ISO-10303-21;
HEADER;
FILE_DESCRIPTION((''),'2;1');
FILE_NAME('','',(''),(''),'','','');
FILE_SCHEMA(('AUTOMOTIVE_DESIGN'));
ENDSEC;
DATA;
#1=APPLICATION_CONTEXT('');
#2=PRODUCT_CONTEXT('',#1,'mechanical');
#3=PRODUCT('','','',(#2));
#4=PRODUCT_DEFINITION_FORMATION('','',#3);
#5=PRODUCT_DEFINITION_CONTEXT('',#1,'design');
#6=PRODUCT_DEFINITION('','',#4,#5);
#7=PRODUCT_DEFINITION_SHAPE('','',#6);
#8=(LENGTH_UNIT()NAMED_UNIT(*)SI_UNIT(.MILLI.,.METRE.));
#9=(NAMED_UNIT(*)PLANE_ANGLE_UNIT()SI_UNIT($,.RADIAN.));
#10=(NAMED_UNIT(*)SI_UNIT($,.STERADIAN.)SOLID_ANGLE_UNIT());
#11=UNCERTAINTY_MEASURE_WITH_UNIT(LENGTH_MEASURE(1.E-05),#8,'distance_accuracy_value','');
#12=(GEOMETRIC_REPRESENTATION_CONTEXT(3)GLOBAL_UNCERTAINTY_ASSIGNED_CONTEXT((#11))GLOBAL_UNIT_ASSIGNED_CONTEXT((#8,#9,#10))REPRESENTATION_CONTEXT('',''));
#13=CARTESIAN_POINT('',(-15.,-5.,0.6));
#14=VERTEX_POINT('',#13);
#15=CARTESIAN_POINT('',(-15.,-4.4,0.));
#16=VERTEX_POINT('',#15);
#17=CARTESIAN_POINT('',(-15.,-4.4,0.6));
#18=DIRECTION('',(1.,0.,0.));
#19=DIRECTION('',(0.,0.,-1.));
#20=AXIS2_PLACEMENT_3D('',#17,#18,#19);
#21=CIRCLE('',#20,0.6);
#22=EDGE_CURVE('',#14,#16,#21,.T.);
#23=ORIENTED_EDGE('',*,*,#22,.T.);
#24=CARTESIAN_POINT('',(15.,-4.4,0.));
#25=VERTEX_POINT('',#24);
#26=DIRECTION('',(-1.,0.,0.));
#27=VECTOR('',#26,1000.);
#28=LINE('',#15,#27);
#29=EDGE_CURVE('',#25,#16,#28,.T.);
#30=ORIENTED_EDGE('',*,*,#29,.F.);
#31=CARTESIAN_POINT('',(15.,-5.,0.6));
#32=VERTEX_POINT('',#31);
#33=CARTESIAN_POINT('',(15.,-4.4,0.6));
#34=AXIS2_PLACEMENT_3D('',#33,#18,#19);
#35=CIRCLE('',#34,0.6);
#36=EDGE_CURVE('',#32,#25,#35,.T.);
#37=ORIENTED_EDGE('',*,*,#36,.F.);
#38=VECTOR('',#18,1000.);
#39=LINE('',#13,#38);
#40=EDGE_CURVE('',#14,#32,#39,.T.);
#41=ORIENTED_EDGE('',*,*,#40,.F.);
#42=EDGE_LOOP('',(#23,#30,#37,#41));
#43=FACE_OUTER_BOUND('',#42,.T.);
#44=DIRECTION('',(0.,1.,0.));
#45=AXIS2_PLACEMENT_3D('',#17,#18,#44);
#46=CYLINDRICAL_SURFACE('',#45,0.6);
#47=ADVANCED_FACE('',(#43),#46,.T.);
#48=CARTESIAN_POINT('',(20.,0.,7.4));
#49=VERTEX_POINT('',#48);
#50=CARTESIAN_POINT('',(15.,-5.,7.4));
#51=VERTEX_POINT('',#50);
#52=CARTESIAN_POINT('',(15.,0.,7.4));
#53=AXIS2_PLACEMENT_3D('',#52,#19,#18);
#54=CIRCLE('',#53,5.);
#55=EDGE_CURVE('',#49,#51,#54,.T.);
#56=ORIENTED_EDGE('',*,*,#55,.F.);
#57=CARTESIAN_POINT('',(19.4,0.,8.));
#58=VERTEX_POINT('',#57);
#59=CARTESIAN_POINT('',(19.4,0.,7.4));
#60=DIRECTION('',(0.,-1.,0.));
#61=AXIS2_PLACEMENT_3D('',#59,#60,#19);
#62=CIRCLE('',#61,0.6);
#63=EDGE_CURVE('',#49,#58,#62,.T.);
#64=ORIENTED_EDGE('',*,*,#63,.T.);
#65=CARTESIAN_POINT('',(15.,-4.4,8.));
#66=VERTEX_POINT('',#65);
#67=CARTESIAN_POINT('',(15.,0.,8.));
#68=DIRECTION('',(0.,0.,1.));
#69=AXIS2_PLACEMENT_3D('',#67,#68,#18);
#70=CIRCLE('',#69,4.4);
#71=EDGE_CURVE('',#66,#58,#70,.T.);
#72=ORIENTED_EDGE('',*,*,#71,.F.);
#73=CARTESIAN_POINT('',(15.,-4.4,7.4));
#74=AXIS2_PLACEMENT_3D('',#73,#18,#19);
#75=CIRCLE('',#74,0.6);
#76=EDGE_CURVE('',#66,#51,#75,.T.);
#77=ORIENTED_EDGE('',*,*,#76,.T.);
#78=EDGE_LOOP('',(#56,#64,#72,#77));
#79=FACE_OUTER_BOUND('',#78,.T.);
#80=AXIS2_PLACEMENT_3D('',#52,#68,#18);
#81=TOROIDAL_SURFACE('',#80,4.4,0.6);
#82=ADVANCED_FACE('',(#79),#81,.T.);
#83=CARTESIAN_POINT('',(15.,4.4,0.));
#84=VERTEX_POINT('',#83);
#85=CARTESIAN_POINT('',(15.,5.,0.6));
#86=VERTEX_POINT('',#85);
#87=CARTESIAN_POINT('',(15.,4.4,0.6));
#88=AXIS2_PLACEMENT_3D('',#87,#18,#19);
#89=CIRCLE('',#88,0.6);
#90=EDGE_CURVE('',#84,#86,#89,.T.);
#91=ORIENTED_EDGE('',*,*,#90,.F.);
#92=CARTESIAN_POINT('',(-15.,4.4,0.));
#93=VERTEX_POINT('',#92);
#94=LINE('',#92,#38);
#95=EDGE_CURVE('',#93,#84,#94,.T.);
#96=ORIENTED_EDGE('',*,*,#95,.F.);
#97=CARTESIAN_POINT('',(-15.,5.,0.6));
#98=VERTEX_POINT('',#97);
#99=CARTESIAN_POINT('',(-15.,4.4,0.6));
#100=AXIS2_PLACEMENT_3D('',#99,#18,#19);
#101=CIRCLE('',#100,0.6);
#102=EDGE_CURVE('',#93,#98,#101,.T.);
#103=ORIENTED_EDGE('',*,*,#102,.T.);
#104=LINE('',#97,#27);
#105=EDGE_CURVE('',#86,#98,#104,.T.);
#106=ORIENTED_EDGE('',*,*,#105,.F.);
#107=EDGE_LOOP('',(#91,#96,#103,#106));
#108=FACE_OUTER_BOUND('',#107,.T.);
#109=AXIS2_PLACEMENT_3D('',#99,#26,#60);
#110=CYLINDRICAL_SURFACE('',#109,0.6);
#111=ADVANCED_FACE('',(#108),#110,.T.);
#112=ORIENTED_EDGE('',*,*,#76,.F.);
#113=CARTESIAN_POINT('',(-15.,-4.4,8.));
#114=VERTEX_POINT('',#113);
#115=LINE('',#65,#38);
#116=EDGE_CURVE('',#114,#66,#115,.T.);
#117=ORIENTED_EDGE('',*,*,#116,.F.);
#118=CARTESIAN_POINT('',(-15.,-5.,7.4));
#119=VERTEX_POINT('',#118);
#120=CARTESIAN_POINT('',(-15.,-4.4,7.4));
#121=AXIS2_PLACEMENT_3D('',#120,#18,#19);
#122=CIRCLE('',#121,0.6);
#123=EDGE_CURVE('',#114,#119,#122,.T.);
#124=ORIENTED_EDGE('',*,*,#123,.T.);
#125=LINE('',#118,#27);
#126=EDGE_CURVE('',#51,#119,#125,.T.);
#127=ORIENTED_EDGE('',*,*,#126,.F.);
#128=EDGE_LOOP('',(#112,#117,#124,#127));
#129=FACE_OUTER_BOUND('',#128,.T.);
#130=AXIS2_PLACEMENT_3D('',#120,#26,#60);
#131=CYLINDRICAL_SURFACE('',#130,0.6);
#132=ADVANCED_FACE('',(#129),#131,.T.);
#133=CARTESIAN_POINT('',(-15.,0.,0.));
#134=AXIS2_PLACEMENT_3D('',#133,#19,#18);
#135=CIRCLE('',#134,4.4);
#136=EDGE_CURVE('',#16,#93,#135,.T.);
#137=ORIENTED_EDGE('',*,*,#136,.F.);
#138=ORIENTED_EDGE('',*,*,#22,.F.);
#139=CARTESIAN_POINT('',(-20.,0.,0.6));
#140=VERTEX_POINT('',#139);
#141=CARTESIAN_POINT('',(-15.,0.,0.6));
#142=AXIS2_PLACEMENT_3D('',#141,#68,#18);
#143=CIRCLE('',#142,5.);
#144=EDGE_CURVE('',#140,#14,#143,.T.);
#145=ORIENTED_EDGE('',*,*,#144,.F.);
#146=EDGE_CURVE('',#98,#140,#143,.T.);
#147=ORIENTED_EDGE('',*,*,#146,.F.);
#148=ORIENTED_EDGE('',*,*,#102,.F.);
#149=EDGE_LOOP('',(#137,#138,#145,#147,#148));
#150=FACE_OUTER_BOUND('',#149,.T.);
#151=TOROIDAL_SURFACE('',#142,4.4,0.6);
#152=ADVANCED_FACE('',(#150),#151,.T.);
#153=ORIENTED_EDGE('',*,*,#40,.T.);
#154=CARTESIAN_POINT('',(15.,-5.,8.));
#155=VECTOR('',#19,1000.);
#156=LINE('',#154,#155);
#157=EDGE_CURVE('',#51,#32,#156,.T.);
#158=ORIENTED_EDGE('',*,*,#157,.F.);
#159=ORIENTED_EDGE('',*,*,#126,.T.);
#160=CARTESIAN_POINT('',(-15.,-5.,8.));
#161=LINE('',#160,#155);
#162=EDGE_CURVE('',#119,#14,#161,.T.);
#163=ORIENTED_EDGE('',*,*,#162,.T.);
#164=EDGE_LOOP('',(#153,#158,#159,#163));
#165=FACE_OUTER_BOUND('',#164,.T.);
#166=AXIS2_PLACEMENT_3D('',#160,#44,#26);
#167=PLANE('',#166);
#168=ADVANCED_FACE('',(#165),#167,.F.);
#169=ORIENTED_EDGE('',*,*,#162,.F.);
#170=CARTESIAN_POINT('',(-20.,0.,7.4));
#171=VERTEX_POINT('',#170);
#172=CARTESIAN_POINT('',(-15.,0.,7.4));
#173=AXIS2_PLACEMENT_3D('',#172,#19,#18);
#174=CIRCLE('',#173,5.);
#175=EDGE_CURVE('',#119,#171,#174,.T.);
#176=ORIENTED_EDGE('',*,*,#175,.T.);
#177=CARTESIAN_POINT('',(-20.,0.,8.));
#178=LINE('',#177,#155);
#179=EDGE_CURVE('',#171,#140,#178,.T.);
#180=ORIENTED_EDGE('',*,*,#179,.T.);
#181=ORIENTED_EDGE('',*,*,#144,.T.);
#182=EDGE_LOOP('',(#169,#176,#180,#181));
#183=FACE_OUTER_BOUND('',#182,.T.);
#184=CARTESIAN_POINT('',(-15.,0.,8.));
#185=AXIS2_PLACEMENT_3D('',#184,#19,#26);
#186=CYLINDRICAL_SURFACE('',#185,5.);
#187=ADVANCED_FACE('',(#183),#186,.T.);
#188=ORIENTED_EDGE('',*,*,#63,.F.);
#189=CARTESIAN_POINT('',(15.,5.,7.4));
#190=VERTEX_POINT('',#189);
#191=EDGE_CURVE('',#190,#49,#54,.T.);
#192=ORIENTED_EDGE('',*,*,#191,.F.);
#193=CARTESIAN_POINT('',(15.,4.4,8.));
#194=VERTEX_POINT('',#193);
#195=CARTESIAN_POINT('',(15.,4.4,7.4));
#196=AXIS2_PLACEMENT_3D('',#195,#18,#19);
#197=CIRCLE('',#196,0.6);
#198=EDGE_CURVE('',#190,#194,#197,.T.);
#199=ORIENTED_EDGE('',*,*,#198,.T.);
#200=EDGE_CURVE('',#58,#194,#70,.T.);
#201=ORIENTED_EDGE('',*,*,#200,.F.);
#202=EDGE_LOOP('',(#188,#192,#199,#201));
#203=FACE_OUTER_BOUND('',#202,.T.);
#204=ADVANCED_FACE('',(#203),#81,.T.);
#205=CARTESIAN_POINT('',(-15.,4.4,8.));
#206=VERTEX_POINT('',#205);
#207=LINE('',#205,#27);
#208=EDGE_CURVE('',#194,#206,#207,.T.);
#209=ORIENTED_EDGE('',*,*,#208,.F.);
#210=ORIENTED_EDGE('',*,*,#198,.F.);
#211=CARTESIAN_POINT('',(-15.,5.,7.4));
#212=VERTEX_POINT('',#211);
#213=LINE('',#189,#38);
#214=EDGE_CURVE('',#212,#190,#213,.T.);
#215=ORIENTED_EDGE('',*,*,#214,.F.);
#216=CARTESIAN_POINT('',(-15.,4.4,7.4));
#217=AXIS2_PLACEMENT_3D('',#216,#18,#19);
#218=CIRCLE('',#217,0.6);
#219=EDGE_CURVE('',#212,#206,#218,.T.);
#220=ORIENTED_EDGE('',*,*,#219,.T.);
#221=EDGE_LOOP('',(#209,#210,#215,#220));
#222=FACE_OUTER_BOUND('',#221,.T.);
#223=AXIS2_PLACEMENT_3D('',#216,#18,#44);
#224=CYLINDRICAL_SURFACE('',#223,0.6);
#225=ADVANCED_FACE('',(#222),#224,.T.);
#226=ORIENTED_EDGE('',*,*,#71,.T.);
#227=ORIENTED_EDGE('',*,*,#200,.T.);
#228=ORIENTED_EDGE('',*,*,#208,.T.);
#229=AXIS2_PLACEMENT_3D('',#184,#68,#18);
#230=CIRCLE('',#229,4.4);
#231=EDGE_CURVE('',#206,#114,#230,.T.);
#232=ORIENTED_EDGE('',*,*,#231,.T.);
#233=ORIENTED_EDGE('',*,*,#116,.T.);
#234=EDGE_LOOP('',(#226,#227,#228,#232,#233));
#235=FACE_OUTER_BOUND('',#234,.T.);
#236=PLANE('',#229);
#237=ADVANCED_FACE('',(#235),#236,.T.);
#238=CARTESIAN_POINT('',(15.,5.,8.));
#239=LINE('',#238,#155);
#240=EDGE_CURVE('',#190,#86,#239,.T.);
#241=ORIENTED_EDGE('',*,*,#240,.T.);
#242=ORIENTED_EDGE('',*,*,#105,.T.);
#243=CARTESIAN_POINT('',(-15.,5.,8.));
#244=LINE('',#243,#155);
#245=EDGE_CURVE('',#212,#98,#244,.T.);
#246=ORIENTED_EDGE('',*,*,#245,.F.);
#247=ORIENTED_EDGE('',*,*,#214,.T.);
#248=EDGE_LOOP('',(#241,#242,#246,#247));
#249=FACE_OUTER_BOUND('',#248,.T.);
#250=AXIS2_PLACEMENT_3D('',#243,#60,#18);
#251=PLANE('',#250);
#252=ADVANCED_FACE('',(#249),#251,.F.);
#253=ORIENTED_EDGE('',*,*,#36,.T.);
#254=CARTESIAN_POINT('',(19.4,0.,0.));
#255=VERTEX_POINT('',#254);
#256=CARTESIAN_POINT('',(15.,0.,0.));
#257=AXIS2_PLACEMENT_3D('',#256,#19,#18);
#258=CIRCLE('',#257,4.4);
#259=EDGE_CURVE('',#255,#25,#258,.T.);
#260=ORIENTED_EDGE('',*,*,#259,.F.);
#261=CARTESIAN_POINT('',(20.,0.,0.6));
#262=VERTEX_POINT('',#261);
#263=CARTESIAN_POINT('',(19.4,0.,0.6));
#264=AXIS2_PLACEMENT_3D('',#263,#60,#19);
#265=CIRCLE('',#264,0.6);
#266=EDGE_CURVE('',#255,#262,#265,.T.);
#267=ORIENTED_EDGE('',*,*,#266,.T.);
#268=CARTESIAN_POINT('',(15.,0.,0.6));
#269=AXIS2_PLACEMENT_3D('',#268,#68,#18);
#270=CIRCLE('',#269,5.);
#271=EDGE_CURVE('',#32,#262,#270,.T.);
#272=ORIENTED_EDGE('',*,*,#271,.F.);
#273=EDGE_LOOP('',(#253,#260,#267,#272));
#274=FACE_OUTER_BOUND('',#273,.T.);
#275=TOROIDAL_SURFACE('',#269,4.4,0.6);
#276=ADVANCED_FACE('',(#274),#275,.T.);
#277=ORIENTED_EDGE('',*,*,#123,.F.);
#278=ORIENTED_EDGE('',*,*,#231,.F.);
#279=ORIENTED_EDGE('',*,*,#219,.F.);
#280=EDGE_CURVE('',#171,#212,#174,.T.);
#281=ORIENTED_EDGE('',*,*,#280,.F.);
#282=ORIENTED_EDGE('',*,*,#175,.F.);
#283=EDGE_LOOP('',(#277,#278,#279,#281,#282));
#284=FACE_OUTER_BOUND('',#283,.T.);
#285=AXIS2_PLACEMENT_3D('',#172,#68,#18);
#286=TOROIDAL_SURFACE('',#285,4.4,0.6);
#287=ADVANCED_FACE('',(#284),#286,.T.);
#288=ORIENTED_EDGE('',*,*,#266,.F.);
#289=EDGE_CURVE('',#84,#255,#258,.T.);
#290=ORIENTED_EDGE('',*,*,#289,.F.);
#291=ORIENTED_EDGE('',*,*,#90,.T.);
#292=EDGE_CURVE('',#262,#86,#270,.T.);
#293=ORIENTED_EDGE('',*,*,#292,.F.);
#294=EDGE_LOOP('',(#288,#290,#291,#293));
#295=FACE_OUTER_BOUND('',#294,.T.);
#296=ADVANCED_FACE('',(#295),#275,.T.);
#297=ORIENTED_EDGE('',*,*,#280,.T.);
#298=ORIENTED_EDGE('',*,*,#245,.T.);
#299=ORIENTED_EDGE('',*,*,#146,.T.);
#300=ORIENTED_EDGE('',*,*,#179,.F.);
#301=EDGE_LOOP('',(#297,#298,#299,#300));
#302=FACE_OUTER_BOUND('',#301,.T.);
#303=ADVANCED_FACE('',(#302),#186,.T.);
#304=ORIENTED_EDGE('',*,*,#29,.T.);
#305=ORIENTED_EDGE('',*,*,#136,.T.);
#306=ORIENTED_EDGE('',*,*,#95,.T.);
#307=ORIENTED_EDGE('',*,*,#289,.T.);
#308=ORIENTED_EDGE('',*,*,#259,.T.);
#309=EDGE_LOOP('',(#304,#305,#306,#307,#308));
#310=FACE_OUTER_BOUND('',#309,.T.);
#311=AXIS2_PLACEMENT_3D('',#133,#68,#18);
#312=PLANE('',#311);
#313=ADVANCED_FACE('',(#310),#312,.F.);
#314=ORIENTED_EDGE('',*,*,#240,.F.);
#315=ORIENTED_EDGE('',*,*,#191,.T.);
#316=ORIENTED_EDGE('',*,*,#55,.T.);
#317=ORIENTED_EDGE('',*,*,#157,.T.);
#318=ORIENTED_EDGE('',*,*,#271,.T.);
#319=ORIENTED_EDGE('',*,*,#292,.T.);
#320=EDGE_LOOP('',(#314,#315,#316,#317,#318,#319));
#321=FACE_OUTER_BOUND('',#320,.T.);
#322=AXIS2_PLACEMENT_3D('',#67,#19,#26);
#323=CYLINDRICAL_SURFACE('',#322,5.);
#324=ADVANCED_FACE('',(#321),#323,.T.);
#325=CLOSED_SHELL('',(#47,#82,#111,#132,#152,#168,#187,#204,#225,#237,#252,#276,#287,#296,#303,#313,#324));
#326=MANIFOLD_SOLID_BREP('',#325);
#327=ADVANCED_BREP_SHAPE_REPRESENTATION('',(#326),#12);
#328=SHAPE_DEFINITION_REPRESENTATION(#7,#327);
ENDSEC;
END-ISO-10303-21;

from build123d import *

# Parameters (mm, degrees)
EXTRUDE_523_DEPTH = 8
FILLET_1_R        = 0.6


with BuildPart() as part:
    # 草图1 → Extrude 523 (new body)
    with BuildSketch(Plane.XY):
        with BuildLine():
            Line((-15, 5), (15, 5))
            ThreePointArc((15, 5), (20, 0), (15, -5))
            Line((15, -5), (-15, -5))
            ThreePointArc((-15, -5), (-20, 0), (-15, 5))
        make_face()
    extrude(amount=EXTRUDE_523_DEPTH)

    # 圆角1
    fillet_1_edges = [part.edges().sort_by_distance(p)[0] for p in [
        (20, 0, 8),
        (0, 5, 8),
        (-20, 0, 8),
        (0, 5, 0),
        (20, 0, 0),
        (0, -5, 0),
        (-20, 0, 0),
        (0, -5, 8),
    ]]
    fillet(fillet_1_edges, radius=FILLET_1_R)


solid = part.part
